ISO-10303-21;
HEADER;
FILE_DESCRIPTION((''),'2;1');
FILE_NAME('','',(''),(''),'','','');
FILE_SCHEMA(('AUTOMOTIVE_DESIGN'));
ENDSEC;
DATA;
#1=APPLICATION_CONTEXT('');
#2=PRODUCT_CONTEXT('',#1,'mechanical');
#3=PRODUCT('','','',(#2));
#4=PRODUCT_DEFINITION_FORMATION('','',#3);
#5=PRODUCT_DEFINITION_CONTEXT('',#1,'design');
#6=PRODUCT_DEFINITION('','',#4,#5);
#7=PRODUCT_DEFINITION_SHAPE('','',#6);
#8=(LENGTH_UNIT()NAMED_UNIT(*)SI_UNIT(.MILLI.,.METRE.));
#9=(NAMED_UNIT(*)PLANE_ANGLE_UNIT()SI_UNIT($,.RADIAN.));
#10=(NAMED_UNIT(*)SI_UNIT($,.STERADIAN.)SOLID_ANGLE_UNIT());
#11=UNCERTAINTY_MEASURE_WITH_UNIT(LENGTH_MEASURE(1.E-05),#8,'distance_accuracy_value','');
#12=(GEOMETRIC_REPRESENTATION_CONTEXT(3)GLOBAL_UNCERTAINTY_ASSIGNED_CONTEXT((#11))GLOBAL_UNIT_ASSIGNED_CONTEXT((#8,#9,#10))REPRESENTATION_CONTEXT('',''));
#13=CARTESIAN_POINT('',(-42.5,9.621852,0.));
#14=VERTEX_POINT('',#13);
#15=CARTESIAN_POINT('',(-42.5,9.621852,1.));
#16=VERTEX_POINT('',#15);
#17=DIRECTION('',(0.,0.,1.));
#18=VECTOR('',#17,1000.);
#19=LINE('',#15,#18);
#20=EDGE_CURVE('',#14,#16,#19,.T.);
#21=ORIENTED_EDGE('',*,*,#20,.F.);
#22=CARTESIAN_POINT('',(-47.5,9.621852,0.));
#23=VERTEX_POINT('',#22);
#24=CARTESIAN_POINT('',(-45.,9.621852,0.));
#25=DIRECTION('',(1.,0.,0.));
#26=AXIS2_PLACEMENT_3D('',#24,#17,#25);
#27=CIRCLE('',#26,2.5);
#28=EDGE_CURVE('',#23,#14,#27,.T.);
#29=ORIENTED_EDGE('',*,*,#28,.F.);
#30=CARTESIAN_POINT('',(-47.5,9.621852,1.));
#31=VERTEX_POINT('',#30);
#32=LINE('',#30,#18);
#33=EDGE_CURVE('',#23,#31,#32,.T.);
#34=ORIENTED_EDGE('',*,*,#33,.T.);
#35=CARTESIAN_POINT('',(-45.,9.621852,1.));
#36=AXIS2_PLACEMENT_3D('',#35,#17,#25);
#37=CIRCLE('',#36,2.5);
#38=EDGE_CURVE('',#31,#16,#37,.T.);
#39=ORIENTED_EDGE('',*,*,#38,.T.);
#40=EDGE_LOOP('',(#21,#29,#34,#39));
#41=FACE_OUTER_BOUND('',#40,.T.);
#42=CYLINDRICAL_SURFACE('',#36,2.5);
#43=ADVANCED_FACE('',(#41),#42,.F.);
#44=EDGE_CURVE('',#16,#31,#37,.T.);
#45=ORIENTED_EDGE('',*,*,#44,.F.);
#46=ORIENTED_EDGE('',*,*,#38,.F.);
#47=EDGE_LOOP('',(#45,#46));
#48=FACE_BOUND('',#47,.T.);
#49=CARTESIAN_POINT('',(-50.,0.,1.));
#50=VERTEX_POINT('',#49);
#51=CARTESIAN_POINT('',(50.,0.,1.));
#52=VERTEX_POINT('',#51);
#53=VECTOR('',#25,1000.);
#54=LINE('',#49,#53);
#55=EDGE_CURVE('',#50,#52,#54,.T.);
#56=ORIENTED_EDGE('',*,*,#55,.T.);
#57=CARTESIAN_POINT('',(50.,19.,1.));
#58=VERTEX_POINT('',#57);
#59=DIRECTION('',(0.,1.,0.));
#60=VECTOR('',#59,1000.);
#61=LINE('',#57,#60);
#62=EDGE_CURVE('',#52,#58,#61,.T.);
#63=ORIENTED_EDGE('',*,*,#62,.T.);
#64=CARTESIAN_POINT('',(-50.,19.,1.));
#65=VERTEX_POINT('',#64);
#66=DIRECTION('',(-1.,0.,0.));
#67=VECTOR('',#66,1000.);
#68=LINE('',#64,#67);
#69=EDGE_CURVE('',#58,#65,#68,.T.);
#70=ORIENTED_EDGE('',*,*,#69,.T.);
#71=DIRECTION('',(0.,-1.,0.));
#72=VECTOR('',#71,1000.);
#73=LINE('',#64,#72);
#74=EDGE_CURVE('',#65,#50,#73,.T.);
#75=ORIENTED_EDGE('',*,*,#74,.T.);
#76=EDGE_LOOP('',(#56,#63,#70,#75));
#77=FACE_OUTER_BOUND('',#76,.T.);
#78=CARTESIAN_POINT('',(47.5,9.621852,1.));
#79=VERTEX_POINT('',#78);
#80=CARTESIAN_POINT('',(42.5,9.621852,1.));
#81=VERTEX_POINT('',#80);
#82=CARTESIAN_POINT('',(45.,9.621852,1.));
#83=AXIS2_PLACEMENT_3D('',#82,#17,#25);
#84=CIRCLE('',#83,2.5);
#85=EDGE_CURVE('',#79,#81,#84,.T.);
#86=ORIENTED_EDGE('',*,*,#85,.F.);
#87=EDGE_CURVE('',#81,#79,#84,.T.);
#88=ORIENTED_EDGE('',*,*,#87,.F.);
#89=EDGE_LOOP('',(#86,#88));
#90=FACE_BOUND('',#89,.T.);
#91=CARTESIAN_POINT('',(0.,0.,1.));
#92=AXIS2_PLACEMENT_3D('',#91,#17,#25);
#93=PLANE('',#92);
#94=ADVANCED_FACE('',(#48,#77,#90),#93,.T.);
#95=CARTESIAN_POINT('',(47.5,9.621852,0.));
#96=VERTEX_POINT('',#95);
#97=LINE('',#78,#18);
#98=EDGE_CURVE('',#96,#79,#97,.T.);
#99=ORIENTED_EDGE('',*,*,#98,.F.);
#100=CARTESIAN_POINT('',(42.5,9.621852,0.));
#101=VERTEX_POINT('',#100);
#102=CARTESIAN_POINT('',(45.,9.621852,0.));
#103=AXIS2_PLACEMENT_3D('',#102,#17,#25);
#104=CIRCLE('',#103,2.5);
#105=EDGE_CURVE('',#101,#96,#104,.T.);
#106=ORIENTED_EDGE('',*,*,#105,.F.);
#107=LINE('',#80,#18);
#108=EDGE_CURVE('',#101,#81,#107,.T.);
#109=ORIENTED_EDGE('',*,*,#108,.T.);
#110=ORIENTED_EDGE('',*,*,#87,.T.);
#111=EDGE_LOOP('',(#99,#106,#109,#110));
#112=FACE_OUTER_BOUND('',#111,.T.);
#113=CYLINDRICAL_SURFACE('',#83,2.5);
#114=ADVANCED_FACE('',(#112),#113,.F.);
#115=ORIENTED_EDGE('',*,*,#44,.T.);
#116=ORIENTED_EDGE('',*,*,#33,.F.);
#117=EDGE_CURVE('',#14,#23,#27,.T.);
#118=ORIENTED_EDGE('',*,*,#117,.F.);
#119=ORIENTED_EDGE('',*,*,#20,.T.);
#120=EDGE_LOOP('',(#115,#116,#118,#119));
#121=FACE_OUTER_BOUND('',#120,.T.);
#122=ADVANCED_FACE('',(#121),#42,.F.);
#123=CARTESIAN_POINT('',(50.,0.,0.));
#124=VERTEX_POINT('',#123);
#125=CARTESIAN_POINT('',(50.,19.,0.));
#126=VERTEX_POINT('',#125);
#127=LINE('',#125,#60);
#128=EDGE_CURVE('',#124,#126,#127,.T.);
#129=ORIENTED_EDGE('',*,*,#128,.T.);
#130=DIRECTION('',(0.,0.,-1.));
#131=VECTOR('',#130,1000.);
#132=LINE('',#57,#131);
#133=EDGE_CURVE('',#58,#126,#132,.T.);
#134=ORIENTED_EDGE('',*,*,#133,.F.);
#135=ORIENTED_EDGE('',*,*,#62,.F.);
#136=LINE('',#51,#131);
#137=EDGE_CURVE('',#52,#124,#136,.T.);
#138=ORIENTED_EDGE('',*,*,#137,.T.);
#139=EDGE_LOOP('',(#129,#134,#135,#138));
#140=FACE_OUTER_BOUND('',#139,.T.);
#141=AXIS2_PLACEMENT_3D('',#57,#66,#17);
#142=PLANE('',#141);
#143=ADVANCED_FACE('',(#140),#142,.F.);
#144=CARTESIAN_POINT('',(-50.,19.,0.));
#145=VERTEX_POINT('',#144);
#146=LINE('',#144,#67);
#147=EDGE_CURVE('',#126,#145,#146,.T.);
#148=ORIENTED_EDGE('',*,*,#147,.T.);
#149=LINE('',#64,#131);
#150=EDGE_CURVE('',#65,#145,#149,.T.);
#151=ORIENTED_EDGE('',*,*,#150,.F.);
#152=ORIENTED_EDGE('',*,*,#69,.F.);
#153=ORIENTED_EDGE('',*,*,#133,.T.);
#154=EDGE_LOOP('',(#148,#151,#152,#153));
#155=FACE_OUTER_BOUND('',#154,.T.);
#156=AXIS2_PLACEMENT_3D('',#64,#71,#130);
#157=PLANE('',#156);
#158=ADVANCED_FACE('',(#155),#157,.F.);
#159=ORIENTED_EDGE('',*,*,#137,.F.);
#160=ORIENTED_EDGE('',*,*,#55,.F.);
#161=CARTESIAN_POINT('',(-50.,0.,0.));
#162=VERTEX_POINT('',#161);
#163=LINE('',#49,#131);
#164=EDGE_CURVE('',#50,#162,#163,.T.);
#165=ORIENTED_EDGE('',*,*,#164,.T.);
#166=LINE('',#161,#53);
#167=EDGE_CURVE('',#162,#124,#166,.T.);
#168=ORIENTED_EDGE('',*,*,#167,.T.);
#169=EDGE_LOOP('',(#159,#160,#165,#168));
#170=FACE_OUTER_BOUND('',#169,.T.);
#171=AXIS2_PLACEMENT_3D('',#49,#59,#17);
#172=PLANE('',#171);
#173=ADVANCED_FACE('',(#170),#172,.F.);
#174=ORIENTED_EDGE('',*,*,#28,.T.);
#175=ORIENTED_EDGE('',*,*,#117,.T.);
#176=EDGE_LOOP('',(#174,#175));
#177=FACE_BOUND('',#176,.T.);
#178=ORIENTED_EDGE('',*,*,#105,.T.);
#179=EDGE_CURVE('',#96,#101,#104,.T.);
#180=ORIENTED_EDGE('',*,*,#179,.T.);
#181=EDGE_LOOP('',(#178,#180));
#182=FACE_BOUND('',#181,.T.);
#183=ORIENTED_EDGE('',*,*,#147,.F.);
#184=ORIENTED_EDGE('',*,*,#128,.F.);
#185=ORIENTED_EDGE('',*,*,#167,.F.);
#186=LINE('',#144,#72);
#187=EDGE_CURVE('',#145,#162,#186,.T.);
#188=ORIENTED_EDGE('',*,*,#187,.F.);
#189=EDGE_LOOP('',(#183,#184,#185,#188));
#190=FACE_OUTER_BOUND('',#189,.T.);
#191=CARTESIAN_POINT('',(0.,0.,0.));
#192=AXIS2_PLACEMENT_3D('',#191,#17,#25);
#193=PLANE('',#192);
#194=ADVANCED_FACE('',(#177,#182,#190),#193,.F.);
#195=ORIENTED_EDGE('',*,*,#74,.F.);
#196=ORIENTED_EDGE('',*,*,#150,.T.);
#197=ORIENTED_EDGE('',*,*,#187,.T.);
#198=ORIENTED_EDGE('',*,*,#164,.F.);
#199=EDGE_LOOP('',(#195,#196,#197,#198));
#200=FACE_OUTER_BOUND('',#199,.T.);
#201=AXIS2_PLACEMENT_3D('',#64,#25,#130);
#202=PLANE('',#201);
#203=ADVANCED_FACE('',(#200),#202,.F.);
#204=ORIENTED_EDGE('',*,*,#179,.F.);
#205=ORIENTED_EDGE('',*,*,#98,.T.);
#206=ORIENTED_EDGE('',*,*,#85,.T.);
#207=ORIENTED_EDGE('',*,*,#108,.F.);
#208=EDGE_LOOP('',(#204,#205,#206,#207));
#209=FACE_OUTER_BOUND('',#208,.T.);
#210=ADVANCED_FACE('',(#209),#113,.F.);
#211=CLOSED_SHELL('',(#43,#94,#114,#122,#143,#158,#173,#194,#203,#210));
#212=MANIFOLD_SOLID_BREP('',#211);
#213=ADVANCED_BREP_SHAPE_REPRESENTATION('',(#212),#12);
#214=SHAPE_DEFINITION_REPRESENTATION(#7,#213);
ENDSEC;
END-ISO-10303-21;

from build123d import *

# Parameters (mm, degrees)
SKETCH_1_W            = 100
SKETCH_1_H            = 19
EXTRUDE_1_DEPTH       = 1
HOLE_WIZARD_5_0_5_1_D = 5


with BuildPart() as part:
    # 草图1 → 凸台-拉伸1 (new body)
    with BuildSketch(Plane.XY):
        with Locations((0, 9.5)):
            Rectangle(SKETCH_1_W, SKETCH_1_H)
    extrude(amount=EXTRUDE_1_DEPTH)

    # Ø5.0 (5) 直径孔1 (through all)
    with Locations(Plane.XY.offset(1)):
        with Locations((-45, 9.621851999), (45, 9.621851999)):
            Hole(HOLE_WIZARD_5_0_5_1_D / 2)


solid = part.part
